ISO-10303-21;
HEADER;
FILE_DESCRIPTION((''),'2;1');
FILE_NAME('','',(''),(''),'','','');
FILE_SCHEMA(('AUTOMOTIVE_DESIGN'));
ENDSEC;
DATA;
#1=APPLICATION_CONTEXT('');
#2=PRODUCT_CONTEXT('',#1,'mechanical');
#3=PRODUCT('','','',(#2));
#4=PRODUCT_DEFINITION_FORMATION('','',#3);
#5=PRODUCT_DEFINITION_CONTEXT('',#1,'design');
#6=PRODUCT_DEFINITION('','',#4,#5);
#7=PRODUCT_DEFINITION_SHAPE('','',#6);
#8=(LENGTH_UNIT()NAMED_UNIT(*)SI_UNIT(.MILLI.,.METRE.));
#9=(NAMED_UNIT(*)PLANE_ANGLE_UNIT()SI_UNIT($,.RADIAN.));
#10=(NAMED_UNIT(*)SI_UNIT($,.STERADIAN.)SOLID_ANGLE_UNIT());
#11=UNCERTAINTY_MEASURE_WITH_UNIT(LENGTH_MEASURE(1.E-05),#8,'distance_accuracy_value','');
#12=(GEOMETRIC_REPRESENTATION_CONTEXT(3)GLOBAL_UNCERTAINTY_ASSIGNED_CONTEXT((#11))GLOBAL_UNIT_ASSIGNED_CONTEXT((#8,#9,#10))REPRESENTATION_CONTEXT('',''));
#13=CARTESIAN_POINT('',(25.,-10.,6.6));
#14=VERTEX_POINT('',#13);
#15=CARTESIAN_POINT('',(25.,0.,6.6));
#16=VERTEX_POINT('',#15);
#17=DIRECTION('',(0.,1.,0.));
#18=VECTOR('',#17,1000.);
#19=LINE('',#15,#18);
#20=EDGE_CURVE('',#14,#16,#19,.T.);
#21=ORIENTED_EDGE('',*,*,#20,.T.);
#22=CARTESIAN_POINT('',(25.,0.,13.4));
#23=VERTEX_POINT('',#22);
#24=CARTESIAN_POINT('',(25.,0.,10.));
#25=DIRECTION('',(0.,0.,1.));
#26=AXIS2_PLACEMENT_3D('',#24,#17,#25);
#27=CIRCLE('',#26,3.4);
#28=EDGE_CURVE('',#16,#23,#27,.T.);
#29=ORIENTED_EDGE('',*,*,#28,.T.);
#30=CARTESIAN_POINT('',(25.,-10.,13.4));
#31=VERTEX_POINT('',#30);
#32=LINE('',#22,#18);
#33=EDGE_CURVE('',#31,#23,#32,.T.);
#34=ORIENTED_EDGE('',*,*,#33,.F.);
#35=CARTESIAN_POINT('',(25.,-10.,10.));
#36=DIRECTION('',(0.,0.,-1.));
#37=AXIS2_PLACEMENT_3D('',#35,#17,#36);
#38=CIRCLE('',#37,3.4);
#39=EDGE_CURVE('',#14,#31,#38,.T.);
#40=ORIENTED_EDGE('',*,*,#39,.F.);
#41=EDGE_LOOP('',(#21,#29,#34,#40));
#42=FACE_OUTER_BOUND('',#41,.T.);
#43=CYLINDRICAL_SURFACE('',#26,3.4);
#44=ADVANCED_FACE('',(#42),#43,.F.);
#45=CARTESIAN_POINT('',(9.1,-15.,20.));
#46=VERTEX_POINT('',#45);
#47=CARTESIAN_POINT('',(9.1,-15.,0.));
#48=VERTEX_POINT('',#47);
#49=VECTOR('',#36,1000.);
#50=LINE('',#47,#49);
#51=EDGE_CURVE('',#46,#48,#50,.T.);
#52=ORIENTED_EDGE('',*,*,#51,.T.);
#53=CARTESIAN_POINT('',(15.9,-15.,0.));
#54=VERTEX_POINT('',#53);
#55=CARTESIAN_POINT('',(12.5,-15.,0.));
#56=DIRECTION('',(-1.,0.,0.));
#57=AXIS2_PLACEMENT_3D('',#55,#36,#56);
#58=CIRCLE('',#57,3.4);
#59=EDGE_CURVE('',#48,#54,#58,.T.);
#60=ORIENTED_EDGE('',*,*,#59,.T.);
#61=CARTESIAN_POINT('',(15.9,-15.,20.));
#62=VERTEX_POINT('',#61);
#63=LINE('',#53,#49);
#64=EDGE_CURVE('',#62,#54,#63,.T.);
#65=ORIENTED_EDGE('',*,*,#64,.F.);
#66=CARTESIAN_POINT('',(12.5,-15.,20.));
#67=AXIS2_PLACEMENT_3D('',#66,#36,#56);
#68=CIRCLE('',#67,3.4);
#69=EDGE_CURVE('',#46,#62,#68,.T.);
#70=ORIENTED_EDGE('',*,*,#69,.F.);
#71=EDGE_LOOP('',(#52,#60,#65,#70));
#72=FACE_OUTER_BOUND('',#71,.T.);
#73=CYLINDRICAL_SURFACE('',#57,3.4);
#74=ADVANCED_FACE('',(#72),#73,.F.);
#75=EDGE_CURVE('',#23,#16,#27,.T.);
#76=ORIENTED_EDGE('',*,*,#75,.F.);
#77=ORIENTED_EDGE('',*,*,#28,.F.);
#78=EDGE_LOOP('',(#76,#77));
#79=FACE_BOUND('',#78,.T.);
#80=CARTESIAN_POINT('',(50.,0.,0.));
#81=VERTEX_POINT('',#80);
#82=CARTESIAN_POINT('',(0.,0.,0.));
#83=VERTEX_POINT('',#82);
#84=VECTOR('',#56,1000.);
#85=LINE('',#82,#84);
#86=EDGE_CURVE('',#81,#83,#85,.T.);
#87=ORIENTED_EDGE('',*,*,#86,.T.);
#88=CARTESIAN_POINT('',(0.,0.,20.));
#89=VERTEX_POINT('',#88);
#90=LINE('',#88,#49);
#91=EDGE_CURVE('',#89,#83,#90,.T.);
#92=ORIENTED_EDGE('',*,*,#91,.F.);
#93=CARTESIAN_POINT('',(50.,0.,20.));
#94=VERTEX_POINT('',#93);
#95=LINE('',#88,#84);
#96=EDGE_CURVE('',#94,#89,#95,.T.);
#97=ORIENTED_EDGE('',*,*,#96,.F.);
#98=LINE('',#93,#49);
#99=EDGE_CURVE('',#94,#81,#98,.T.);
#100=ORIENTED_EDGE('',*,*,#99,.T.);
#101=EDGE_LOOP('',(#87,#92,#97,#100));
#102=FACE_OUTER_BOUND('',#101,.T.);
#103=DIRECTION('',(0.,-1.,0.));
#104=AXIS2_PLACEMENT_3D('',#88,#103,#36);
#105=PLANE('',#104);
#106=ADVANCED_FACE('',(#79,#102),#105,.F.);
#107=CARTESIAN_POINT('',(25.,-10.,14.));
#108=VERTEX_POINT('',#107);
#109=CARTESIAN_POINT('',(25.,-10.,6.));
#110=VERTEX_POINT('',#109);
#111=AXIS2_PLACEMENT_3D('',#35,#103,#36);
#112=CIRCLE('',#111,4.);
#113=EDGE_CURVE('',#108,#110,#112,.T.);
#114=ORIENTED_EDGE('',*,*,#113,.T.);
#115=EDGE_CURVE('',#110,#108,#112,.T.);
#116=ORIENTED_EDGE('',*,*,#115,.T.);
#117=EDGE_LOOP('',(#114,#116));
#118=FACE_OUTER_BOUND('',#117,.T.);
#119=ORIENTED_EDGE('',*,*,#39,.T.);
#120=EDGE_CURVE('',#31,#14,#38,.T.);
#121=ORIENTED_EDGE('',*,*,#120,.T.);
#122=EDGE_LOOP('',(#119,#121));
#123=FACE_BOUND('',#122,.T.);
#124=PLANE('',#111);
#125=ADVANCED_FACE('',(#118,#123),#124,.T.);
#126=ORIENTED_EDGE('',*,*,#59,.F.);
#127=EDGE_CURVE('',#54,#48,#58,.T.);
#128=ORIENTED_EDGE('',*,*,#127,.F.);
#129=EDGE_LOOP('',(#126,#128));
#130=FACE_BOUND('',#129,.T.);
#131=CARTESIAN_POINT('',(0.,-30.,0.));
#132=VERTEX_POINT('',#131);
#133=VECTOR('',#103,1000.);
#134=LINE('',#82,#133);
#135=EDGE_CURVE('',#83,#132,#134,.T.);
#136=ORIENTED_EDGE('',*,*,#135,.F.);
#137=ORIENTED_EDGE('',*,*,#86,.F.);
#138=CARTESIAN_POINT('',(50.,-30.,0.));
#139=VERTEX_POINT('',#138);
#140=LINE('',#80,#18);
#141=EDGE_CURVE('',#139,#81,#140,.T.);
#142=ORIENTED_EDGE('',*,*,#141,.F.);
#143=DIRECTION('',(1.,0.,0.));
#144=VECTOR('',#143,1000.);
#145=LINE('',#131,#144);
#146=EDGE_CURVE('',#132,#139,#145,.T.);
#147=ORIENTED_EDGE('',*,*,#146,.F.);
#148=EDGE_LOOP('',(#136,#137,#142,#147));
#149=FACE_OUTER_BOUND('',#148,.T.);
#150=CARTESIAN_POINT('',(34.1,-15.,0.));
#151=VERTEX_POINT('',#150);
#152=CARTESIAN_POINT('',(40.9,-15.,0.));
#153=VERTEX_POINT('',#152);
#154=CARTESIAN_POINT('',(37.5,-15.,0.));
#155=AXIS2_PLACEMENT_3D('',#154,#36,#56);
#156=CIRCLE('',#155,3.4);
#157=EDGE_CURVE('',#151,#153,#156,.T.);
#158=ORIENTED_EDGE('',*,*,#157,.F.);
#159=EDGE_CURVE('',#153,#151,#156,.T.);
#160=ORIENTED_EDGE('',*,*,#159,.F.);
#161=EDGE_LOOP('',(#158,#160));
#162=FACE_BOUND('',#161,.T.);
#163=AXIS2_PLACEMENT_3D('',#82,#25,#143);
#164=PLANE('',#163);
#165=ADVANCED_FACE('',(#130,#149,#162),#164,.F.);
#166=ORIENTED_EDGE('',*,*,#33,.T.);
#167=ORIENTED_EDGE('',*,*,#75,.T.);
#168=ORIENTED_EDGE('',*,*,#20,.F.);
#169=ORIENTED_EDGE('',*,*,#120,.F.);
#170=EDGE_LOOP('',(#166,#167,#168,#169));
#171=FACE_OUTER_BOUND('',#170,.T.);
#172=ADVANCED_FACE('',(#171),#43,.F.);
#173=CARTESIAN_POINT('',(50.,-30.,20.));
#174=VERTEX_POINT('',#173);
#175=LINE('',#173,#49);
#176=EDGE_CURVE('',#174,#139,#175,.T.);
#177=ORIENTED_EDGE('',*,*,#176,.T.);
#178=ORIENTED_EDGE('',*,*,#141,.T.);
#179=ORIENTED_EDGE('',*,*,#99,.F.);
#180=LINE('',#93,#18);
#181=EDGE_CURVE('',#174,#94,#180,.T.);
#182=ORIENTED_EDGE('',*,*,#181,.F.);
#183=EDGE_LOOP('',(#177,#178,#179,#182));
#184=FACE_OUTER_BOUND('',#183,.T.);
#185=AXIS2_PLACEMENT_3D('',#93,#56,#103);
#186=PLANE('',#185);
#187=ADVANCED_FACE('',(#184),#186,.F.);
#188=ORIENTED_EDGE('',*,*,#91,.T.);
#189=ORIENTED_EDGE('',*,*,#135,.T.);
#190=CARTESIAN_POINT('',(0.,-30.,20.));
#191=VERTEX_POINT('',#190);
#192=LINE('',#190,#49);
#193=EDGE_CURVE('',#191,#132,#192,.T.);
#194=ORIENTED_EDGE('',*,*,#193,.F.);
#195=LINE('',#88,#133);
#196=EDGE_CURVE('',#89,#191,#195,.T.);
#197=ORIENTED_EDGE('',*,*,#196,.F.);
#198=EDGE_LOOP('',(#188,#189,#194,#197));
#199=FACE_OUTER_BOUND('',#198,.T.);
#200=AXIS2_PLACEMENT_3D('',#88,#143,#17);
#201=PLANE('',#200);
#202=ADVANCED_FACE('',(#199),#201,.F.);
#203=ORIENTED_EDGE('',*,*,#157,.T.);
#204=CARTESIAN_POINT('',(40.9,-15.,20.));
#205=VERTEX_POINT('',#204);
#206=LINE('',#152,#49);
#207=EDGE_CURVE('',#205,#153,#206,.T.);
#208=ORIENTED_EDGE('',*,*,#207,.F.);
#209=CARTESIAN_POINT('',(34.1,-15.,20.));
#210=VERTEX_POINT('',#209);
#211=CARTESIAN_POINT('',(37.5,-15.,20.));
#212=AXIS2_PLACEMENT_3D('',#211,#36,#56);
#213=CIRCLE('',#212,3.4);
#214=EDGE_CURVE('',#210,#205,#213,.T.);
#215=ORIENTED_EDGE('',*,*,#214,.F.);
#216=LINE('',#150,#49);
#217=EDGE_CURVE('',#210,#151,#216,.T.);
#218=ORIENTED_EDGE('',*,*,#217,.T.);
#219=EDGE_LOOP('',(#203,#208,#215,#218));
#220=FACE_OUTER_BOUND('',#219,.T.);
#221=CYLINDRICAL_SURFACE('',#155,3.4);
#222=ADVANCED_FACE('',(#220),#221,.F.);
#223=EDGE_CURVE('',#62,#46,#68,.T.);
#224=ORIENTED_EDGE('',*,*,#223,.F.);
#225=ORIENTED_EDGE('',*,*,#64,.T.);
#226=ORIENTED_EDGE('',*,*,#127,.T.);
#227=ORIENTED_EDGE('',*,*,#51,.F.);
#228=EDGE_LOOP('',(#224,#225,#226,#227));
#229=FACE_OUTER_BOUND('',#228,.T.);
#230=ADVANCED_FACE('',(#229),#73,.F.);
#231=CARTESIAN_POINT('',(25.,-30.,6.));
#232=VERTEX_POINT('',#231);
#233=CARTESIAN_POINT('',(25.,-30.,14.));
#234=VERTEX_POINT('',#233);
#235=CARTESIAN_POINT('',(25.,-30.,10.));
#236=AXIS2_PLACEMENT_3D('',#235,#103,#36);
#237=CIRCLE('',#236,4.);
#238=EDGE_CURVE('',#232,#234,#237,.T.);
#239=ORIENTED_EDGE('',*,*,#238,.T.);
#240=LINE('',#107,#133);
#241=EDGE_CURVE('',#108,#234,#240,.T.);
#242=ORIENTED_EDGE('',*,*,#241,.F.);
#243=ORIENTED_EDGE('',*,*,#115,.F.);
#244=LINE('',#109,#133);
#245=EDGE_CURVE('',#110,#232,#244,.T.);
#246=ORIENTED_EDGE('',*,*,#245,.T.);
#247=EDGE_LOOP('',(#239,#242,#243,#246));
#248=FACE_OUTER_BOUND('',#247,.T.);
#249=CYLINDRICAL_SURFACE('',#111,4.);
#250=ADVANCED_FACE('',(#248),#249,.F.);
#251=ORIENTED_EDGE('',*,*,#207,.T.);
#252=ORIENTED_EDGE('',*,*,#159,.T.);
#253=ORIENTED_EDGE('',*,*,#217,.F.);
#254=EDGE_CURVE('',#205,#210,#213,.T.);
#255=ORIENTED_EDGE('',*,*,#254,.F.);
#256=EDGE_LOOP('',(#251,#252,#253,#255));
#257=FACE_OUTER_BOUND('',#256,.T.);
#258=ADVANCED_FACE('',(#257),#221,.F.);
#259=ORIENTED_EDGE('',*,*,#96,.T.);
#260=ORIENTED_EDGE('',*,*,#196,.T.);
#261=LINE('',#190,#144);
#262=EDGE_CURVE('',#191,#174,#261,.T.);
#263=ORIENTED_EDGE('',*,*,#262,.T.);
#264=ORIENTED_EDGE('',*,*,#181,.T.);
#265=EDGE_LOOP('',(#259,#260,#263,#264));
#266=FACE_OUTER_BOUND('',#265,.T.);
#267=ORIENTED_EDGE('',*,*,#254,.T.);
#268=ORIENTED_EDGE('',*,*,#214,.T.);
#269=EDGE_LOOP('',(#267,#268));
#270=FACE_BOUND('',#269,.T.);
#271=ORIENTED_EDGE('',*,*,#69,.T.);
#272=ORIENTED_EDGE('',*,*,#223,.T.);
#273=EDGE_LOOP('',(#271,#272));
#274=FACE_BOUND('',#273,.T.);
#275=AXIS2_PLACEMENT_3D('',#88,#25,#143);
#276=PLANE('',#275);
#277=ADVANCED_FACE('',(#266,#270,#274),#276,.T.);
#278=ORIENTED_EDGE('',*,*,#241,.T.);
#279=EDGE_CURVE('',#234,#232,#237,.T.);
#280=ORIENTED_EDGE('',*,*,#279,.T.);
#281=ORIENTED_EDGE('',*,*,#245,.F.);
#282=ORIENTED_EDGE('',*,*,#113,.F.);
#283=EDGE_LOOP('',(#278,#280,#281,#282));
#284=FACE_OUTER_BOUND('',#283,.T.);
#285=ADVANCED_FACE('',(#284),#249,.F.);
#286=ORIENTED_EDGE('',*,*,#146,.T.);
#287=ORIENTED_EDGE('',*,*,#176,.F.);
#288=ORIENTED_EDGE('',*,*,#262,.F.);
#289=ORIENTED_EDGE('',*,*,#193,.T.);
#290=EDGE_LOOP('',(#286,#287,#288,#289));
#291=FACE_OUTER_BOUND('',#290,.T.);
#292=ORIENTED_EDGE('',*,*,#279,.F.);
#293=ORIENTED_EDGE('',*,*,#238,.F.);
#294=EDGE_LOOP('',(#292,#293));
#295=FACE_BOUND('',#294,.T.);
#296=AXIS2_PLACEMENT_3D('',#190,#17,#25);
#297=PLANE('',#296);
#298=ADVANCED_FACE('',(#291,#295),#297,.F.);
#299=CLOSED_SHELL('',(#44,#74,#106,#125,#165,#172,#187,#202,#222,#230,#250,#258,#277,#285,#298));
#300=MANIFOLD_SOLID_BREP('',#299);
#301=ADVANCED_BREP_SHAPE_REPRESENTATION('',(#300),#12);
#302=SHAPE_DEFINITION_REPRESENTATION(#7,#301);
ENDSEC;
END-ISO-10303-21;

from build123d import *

# Parameters (mm, degrees)
SKETCH1_W           = 50
SKETCH1_H           = 30
BOSS_EXTRUDE1_DEPTH = 20
M8_TAPPED_HOLE1_D   = 6.8
M8_TAPPED_HOLE2_D   = 6.8
SKETCH6_R           = 4
CUT_EXTRUDE1_DEPTH  = 20


with BuildPart() as part:
    # Sketch1 → Boss-Extrude1 (new body)
    with BuildSketch(Plane.XY):
        with Locations((25, -15)):
            Rectangle(SKETCH1_W, SKETCH1_H)
    extrude(amount=BOSS_EXTRUDE1_DEPTH)

    # M8 Tapped Hole1 (through all)
    with Locations(Plane(origin=(0, 0, 0), x_dir=(-1, 0, 0), z_dir=(0, 0, -1))):
        with Locations((-12.5, -15), (-37.5, -15)):
            Hole(M8_TAPPED_HOLE1_D / 2)

    # M8 Tapped Hole2 (through all)
    with Locations(Plane(origin=(25, 0, 10), x_dir=(0, 0, 1), z_dir=(0, 1, 0))):
        with Locations((0, 0)):
            Hole(M8_TAPPED_HOLE2_D / 2)

    # Sketch6 → Cut-Extrude1 (cut)
    with BuildSketch(Plane.XZ.offset(30)):
        with Locations(Location((25, 10, 0), (0, 0, 270))):
            Circle(SKETCH6_R)
    extrude(amount=-CUT_EXTRUDE1_DEPTH, mode=Mode.SUBTRACT)


solid = part.part
